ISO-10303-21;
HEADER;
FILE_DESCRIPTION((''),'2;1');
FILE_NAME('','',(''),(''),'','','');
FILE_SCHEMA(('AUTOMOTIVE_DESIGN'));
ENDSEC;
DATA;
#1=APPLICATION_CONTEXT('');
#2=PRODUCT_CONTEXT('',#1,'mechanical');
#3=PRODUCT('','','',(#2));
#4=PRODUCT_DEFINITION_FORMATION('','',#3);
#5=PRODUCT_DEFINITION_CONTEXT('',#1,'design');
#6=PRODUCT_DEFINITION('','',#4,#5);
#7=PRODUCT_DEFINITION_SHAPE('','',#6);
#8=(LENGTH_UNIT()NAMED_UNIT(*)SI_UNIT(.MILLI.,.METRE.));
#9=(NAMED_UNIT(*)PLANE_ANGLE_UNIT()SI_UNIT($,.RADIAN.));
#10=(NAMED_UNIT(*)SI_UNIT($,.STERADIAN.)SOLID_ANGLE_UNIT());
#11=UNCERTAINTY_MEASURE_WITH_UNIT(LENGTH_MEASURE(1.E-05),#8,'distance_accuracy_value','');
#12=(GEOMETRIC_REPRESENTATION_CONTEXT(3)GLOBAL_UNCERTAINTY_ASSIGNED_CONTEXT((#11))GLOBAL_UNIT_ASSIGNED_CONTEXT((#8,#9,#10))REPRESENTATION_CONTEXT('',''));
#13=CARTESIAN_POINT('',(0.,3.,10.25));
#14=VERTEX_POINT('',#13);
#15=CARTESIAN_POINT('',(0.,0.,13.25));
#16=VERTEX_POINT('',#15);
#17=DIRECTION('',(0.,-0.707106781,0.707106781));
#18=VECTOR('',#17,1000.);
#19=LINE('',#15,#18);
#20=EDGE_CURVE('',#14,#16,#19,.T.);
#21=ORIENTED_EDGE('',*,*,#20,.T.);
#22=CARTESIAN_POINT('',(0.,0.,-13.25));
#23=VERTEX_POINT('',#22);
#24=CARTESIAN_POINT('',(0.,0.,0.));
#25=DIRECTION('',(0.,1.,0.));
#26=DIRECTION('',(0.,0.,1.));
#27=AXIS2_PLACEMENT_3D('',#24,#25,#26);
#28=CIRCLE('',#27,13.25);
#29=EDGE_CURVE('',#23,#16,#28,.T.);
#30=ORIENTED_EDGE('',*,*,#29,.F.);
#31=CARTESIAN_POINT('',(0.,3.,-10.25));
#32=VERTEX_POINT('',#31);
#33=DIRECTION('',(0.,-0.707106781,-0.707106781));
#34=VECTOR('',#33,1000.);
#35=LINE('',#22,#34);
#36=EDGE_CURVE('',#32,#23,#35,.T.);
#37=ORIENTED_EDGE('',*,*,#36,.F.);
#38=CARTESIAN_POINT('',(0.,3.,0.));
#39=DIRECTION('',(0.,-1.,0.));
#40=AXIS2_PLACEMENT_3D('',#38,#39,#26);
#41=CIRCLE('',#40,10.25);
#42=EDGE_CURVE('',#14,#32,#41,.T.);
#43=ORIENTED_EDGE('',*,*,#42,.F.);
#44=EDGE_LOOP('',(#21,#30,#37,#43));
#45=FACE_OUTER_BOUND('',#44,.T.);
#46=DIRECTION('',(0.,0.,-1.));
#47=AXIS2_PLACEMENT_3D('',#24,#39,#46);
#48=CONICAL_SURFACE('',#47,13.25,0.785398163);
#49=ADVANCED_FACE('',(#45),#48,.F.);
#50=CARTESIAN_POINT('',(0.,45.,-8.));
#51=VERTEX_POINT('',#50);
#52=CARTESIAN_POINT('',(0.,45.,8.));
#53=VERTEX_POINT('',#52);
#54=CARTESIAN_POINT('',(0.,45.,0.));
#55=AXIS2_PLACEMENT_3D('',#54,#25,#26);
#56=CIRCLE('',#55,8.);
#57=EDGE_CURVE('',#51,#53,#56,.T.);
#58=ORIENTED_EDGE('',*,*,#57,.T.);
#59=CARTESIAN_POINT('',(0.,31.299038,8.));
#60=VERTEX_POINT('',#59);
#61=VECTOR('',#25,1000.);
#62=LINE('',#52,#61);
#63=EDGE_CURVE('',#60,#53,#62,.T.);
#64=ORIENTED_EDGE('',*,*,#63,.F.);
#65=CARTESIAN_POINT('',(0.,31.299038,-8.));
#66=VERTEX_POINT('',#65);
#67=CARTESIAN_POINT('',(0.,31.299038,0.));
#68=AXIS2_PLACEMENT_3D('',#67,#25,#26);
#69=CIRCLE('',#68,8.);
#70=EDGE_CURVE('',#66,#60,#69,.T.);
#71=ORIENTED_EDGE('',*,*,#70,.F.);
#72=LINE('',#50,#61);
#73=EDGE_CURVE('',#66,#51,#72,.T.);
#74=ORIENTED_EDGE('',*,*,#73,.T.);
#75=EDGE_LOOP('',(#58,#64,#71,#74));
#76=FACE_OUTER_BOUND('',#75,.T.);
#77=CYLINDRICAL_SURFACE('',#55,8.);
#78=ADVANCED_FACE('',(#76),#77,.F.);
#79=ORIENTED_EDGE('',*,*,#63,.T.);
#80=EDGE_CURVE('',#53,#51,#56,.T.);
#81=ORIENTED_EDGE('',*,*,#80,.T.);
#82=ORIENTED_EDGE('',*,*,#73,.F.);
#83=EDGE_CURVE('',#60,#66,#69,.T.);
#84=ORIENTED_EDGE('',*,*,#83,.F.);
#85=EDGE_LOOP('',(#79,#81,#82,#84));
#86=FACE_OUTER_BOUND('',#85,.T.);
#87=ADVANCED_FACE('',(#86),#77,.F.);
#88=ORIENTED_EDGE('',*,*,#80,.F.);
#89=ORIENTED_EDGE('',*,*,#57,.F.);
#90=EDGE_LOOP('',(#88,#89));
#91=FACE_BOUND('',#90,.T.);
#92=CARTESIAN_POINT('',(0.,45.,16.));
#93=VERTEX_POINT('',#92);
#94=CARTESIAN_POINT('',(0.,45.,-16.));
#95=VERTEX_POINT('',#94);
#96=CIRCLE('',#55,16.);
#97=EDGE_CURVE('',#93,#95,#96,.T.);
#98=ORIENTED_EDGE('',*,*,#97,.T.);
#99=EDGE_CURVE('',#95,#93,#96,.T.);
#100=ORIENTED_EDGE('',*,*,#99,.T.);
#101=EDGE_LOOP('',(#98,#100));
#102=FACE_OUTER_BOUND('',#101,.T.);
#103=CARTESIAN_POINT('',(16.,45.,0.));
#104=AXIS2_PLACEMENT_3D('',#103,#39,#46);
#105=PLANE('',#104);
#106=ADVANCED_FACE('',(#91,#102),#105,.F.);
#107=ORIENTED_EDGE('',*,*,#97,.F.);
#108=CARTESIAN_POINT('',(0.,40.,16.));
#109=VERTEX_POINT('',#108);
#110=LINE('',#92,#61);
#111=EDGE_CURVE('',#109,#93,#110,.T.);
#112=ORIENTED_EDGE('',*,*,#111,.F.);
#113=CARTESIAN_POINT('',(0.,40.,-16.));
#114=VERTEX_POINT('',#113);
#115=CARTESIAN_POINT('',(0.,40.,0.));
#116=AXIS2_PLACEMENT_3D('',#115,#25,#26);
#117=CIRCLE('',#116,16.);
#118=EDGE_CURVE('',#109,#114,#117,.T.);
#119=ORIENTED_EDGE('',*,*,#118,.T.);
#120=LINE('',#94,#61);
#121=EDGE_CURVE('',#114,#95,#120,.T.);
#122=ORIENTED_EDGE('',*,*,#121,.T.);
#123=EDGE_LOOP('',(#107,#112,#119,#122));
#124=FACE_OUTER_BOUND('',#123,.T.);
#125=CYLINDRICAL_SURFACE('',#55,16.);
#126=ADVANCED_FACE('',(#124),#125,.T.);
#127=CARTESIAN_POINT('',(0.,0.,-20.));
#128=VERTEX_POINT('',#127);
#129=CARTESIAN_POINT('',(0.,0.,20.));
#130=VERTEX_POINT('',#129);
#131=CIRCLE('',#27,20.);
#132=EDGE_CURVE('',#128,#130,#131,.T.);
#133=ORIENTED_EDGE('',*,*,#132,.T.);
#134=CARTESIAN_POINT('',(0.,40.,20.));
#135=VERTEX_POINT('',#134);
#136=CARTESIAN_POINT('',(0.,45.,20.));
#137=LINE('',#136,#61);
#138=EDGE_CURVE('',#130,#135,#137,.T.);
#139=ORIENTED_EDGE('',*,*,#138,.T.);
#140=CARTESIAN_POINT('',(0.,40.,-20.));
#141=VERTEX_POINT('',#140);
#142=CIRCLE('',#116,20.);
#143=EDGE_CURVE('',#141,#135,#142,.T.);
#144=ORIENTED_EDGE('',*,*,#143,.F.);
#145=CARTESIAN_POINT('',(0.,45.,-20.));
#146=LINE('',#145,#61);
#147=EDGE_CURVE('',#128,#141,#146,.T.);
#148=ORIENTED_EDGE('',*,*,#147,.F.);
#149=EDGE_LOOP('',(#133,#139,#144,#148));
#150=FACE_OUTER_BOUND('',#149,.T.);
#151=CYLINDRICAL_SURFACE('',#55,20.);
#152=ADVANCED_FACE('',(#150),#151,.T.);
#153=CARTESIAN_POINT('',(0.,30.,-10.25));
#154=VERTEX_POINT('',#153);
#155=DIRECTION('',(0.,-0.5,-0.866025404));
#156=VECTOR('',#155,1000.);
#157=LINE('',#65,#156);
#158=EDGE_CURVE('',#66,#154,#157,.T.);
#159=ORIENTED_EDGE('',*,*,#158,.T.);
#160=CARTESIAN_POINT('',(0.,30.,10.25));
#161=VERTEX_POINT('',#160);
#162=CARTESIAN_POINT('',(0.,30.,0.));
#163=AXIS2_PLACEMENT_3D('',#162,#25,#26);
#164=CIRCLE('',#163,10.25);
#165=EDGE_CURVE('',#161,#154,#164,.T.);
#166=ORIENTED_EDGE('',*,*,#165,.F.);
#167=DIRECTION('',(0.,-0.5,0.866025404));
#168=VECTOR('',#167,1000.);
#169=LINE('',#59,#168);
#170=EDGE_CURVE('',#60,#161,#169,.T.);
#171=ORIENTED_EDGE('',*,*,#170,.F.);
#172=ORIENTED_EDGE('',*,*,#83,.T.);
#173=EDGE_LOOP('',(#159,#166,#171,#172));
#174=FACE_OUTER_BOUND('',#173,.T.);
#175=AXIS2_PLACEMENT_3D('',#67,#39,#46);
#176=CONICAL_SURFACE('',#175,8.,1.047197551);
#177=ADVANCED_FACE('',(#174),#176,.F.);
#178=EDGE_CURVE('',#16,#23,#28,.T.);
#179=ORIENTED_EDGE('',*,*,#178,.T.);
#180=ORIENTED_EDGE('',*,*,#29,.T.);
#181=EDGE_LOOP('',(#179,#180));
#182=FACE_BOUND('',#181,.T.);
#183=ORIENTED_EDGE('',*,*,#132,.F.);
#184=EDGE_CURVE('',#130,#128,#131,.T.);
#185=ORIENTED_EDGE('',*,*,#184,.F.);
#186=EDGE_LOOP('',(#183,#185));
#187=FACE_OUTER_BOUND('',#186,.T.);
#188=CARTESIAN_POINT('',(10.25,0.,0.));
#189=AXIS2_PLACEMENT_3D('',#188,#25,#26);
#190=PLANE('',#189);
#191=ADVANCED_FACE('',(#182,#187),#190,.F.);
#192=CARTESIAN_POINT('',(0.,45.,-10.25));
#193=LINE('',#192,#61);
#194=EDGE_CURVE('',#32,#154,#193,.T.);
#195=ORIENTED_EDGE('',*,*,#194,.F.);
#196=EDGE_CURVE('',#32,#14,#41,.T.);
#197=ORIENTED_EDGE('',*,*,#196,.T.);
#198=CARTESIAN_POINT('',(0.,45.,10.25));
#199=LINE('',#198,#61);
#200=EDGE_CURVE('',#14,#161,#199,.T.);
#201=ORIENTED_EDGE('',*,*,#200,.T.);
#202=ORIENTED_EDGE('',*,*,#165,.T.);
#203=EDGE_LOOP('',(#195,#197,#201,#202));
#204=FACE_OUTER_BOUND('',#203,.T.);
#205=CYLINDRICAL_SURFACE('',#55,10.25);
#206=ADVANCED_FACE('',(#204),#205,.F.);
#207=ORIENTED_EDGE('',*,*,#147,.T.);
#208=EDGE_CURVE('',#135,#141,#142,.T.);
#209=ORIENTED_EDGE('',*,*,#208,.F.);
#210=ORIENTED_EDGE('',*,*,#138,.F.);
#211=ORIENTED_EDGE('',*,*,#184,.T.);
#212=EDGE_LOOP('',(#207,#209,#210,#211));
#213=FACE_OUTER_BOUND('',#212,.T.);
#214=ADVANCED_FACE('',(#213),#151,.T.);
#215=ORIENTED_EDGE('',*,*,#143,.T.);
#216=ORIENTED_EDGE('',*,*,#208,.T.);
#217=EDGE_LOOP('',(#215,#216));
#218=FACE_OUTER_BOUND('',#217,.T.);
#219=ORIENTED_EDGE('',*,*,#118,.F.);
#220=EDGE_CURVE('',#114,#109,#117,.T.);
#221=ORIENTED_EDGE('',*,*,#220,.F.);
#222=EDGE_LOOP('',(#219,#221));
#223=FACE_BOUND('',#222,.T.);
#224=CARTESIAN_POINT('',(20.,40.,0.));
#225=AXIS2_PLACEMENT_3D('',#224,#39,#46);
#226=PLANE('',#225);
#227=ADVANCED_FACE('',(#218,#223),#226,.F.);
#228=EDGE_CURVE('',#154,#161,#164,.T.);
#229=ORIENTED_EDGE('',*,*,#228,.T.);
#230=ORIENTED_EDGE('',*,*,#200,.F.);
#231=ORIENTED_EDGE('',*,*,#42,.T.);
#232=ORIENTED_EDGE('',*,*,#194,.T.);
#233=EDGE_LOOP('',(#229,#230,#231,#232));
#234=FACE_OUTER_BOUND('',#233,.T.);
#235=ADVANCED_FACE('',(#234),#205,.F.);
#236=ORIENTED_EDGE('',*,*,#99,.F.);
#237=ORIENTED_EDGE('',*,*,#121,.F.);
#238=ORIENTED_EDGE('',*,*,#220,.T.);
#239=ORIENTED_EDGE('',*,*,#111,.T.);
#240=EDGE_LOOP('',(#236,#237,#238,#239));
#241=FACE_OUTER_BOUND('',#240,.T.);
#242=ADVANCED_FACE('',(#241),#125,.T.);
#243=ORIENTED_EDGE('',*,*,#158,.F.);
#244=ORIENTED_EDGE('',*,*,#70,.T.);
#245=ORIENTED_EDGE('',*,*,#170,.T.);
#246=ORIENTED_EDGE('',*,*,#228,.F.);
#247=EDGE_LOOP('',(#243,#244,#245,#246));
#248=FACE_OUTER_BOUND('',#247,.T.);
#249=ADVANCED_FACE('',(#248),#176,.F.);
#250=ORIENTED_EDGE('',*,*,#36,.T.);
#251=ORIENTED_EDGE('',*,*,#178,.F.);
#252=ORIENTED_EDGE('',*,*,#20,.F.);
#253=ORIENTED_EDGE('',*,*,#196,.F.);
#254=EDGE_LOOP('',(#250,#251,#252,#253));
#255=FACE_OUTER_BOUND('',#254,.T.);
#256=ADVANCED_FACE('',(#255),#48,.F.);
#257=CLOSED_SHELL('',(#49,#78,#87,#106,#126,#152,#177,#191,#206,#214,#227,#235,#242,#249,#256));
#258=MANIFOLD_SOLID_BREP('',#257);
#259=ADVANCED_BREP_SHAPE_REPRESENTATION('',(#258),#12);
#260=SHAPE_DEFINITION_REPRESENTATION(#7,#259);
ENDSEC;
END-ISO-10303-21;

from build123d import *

# Parameters (mm, degrees)
CHAMFER1_SIZE = 3


with BuildPart() as part:
    # Sketch1 → Revolve1 (revolve)
    with BuildSketch(Plane.XY, mode=Mode.PRIVATE) as revolve1_sk:
        Polygon((10.25, 0), (20, 0), (20, 40), (16, 40), (16, 45), (8, 45), (8, 31.299038106), (10.25, 30), align=None)
    revolve(revolve1_sk.sketch.rotate(Axis((0, 45, 0), (0, -1, 0)), 90), axis=Axis((0, 45, 0), (0, -1, 0)))

    # Chamfer1
    chamfer1_edges = [part.edges().sort_by_distance(p)[0] for p in [
        (0, 0, -10.25),
    ]]
    chamfer(chamfer1_edges, length=CHAMFER1_SIZE)


solid = part.part
